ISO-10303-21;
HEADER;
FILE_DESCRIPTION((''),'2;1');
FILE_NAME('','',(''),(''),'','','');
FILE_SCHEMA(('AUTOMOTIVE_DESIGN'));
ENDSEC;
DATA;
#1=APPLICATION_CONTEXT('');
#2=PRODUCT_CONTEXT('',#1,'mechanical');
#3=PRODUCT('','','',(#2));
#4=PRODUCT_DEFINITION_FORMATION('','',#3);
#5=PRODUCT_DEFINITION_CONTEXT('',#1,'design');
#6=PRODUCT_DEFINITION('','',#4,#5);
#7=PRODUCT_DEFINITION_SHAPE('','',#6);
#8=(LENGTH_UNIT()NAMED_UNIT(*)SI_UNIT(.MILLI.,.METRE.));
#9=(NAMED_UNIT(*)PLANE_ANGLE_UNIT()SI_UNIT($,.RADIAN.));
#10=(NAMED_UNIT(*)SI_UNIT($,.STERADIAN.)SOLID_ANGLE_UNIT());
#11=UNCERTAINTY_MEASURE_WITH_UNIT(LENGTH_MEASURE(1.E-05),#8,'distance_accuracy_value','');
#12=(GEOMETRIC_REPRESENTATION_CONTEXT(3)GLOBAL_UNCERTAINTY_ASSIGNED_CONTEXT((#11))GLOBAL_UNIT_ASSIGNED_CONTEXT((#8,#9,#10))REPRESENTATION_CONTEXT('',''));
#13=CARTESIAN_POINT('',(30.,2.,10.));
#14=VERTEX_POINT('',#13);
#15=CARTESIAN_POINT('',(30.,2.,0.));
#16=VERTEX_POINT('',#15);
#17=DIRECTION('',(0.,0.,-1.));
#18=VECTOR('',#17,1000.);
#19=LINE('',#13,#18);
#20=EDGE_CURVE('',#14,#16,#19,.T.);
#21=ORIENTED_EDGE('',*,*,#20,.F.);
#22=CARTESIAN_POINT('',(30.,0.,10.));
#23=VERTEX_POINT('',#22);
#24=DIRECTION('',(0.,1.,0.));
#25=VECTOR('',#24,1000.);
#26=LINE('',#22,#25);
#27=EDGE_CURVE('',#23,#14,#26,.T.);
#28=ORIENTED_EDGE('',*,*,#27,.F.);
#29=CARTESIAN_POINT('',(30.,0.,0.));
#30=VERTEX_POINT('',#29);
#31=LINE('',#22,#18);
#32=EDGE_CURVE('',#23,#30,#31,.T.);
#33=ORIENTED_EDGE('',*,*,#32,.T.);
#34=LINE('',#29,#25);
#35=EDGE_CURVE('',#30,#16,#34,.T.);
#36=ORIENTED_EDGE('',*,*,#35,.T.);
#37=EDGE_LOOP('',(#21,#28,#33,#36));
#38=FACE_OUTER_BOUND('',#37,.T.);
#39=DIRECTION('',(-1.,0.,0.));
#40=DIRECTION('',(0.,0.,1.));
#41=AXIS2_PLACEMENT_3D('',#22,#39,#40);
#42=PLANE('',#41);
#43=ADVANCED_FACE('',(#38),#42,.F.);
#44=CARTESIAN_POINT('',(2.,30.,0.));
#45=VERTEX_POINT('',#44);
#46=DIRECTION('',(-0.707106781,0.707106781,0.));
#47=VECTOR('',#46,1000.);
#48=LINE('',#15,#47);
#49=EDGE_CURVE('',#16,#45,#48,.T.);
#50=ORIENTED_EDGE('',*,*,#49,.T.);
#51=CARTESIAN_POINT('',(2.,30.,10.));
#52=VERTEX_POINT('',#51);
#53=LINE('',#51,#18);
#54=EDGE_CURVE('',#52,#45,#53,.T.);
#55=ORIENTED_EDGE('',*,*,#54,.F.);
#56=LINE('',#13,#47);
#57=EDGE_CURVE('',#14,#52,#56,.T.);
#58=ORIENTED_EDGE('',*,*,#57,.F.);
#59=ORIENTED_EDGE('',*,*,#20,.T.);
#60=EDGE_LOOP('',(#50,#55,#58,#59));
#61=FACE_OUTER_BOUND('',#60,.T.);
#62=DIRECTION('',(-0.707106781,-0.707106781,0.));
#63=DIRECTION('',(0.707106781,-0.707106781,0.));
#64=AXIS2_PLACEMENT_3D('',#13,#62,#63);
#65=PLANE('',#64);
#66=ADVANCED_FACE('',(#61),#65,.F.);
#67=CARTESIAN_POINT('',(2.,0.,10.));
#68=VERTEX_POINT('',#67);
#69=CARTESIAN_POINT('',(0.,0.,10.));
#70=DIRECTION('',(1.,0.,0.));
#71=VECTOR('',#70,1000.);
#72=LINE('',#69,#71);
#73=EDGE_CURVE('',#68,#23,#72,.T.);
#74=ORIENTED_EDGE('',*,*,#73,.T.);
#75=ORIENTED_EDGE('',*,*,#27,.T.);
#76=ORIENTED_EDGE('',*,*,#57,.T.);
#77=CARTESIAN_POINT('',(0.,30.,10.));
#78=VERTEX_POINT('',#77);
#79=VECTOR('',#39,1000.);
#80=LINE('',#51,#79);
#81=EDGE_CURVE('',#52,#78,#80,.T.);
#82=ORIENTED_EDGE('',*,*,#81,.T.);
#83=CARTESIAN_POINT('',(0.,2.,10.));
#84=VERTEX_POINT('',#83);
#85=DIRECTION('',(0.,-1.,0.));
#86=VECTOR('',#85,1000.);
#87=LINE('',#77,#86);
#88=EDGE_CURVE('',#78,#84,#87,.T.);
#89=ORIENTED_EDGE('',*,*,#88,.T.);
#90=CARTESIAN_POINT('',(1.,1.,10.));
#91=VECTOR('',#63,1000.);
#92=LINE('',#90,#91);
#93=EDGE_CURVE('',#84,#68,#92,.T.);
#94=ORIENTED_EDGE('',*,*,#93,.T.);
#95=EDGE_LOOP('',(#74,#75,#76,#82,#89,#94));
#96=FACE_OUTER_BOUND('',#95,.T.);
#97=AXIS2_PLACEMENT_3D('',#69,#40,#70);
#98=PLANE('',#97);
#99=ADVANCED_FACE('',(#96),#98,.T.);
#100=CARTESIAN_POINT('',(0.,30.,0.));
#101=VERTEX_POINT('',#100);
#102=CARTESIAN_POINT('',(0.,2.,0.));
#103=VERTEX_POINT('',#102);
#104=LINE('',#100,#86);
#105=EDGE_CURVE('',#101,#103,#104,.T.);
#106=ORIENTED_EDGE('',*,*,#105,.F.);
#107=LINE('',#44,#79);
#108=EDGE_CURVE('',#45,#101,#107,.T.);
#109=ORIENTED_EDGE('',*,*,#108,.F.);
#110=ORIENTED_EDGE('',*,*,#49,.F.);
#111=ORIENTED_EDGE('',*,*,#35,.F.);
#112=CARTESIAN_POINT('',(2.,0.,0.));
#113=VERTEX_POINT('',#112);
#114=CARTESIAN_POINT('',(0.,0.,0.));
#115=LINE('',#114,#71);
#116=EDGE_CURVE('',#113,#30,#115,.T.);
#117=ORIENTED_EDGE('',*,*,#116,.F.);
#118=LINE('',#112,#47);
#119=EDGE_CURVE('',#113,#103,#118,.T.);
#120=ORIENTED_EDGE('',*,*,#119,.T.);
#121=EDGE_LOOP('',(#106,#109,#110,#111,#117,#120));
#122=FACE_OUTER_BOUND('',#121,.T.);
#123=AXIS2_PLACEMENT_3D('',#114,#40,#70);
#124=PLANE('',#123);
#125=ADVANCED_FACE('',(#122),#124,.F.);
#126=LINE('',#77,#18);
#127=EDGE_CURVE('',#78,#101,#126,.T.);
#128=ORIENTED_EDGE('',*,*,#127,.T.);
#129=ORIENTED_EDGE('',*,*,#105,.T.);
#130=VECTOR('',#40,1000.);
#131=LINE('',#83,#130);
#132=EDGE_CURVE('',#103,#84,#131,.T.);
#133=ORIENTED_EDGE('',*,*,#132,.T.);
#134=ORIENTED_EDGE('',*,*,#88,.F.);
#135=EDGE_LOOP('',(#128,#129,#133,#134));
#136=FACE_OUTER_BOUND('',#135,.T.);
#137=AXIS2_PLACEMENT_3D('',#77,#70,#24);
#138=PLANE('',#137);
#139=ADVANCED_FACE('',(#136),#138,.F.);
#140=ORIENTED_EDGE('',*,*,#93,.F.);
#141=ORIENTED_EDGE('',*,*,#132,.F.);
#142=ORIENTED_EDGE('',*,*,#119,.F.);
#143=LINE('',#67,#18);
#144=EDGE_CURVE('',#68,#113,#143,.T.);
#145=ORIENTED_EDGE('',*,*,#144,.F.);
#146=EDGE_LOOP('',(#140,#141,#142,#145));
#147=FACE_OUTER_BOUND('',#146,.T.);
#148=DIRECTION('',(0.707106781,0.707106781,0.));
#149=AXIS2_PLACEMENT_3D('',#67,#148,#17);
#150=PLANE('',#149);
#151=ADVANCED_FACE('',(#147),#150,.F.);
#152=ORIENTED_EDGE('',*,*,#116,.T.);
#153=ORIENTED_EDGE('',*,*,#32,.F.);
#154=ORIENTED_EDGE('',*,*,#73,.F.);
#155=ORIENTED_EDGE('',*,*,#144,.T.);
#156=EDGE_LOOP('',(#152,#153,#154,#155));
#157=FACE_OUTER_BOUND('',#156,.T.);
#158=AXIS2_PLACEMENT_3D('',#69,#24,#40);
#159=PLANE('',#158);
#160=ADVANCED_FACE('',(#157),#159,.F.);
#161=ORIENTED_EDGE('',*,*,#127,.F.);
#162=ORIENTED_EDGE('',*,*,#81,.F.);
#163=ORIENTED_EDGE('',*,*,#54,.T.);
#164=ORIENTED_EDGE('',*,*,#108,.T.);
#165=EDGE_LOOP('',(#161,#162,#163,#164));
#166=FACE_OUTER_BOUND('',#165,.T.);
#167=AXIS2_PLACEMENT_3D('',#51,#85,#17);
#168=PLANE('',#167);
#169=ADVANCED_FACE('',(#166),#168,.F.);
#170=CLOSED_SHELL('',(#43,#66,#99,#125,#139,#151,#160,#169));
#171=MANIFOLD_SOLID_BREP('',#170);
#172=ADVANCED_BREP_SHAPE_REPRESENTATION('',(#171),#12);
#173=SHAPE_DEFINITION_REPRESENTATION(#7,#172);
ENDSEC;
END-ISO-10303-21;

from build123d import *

# Parameters (mm, degrees)
EXTRUDE_1_DEPTH = 10
CHAMFER_1_SIZE  = 2


with BuildPart() as part:
    # 草图1 → 凸台-拉伸1 (new body)
    with BuildSketch(Plane.XY):
        Polygon((0, 30), (0, 0), (30, 0), (30, 2), (2, 30), align=None)
    extrude(amount=EXTRUDE_1_DEPTH)

    # 倒角1
    chamfer_1_edges = [part.edges().sort_by_distance(p)[0] for p in [
        (0, 0, 5),
    ]]
    chamfer(chamfer_1_edges, length=CHAMFER_1_SIZE)


solid = part.part
